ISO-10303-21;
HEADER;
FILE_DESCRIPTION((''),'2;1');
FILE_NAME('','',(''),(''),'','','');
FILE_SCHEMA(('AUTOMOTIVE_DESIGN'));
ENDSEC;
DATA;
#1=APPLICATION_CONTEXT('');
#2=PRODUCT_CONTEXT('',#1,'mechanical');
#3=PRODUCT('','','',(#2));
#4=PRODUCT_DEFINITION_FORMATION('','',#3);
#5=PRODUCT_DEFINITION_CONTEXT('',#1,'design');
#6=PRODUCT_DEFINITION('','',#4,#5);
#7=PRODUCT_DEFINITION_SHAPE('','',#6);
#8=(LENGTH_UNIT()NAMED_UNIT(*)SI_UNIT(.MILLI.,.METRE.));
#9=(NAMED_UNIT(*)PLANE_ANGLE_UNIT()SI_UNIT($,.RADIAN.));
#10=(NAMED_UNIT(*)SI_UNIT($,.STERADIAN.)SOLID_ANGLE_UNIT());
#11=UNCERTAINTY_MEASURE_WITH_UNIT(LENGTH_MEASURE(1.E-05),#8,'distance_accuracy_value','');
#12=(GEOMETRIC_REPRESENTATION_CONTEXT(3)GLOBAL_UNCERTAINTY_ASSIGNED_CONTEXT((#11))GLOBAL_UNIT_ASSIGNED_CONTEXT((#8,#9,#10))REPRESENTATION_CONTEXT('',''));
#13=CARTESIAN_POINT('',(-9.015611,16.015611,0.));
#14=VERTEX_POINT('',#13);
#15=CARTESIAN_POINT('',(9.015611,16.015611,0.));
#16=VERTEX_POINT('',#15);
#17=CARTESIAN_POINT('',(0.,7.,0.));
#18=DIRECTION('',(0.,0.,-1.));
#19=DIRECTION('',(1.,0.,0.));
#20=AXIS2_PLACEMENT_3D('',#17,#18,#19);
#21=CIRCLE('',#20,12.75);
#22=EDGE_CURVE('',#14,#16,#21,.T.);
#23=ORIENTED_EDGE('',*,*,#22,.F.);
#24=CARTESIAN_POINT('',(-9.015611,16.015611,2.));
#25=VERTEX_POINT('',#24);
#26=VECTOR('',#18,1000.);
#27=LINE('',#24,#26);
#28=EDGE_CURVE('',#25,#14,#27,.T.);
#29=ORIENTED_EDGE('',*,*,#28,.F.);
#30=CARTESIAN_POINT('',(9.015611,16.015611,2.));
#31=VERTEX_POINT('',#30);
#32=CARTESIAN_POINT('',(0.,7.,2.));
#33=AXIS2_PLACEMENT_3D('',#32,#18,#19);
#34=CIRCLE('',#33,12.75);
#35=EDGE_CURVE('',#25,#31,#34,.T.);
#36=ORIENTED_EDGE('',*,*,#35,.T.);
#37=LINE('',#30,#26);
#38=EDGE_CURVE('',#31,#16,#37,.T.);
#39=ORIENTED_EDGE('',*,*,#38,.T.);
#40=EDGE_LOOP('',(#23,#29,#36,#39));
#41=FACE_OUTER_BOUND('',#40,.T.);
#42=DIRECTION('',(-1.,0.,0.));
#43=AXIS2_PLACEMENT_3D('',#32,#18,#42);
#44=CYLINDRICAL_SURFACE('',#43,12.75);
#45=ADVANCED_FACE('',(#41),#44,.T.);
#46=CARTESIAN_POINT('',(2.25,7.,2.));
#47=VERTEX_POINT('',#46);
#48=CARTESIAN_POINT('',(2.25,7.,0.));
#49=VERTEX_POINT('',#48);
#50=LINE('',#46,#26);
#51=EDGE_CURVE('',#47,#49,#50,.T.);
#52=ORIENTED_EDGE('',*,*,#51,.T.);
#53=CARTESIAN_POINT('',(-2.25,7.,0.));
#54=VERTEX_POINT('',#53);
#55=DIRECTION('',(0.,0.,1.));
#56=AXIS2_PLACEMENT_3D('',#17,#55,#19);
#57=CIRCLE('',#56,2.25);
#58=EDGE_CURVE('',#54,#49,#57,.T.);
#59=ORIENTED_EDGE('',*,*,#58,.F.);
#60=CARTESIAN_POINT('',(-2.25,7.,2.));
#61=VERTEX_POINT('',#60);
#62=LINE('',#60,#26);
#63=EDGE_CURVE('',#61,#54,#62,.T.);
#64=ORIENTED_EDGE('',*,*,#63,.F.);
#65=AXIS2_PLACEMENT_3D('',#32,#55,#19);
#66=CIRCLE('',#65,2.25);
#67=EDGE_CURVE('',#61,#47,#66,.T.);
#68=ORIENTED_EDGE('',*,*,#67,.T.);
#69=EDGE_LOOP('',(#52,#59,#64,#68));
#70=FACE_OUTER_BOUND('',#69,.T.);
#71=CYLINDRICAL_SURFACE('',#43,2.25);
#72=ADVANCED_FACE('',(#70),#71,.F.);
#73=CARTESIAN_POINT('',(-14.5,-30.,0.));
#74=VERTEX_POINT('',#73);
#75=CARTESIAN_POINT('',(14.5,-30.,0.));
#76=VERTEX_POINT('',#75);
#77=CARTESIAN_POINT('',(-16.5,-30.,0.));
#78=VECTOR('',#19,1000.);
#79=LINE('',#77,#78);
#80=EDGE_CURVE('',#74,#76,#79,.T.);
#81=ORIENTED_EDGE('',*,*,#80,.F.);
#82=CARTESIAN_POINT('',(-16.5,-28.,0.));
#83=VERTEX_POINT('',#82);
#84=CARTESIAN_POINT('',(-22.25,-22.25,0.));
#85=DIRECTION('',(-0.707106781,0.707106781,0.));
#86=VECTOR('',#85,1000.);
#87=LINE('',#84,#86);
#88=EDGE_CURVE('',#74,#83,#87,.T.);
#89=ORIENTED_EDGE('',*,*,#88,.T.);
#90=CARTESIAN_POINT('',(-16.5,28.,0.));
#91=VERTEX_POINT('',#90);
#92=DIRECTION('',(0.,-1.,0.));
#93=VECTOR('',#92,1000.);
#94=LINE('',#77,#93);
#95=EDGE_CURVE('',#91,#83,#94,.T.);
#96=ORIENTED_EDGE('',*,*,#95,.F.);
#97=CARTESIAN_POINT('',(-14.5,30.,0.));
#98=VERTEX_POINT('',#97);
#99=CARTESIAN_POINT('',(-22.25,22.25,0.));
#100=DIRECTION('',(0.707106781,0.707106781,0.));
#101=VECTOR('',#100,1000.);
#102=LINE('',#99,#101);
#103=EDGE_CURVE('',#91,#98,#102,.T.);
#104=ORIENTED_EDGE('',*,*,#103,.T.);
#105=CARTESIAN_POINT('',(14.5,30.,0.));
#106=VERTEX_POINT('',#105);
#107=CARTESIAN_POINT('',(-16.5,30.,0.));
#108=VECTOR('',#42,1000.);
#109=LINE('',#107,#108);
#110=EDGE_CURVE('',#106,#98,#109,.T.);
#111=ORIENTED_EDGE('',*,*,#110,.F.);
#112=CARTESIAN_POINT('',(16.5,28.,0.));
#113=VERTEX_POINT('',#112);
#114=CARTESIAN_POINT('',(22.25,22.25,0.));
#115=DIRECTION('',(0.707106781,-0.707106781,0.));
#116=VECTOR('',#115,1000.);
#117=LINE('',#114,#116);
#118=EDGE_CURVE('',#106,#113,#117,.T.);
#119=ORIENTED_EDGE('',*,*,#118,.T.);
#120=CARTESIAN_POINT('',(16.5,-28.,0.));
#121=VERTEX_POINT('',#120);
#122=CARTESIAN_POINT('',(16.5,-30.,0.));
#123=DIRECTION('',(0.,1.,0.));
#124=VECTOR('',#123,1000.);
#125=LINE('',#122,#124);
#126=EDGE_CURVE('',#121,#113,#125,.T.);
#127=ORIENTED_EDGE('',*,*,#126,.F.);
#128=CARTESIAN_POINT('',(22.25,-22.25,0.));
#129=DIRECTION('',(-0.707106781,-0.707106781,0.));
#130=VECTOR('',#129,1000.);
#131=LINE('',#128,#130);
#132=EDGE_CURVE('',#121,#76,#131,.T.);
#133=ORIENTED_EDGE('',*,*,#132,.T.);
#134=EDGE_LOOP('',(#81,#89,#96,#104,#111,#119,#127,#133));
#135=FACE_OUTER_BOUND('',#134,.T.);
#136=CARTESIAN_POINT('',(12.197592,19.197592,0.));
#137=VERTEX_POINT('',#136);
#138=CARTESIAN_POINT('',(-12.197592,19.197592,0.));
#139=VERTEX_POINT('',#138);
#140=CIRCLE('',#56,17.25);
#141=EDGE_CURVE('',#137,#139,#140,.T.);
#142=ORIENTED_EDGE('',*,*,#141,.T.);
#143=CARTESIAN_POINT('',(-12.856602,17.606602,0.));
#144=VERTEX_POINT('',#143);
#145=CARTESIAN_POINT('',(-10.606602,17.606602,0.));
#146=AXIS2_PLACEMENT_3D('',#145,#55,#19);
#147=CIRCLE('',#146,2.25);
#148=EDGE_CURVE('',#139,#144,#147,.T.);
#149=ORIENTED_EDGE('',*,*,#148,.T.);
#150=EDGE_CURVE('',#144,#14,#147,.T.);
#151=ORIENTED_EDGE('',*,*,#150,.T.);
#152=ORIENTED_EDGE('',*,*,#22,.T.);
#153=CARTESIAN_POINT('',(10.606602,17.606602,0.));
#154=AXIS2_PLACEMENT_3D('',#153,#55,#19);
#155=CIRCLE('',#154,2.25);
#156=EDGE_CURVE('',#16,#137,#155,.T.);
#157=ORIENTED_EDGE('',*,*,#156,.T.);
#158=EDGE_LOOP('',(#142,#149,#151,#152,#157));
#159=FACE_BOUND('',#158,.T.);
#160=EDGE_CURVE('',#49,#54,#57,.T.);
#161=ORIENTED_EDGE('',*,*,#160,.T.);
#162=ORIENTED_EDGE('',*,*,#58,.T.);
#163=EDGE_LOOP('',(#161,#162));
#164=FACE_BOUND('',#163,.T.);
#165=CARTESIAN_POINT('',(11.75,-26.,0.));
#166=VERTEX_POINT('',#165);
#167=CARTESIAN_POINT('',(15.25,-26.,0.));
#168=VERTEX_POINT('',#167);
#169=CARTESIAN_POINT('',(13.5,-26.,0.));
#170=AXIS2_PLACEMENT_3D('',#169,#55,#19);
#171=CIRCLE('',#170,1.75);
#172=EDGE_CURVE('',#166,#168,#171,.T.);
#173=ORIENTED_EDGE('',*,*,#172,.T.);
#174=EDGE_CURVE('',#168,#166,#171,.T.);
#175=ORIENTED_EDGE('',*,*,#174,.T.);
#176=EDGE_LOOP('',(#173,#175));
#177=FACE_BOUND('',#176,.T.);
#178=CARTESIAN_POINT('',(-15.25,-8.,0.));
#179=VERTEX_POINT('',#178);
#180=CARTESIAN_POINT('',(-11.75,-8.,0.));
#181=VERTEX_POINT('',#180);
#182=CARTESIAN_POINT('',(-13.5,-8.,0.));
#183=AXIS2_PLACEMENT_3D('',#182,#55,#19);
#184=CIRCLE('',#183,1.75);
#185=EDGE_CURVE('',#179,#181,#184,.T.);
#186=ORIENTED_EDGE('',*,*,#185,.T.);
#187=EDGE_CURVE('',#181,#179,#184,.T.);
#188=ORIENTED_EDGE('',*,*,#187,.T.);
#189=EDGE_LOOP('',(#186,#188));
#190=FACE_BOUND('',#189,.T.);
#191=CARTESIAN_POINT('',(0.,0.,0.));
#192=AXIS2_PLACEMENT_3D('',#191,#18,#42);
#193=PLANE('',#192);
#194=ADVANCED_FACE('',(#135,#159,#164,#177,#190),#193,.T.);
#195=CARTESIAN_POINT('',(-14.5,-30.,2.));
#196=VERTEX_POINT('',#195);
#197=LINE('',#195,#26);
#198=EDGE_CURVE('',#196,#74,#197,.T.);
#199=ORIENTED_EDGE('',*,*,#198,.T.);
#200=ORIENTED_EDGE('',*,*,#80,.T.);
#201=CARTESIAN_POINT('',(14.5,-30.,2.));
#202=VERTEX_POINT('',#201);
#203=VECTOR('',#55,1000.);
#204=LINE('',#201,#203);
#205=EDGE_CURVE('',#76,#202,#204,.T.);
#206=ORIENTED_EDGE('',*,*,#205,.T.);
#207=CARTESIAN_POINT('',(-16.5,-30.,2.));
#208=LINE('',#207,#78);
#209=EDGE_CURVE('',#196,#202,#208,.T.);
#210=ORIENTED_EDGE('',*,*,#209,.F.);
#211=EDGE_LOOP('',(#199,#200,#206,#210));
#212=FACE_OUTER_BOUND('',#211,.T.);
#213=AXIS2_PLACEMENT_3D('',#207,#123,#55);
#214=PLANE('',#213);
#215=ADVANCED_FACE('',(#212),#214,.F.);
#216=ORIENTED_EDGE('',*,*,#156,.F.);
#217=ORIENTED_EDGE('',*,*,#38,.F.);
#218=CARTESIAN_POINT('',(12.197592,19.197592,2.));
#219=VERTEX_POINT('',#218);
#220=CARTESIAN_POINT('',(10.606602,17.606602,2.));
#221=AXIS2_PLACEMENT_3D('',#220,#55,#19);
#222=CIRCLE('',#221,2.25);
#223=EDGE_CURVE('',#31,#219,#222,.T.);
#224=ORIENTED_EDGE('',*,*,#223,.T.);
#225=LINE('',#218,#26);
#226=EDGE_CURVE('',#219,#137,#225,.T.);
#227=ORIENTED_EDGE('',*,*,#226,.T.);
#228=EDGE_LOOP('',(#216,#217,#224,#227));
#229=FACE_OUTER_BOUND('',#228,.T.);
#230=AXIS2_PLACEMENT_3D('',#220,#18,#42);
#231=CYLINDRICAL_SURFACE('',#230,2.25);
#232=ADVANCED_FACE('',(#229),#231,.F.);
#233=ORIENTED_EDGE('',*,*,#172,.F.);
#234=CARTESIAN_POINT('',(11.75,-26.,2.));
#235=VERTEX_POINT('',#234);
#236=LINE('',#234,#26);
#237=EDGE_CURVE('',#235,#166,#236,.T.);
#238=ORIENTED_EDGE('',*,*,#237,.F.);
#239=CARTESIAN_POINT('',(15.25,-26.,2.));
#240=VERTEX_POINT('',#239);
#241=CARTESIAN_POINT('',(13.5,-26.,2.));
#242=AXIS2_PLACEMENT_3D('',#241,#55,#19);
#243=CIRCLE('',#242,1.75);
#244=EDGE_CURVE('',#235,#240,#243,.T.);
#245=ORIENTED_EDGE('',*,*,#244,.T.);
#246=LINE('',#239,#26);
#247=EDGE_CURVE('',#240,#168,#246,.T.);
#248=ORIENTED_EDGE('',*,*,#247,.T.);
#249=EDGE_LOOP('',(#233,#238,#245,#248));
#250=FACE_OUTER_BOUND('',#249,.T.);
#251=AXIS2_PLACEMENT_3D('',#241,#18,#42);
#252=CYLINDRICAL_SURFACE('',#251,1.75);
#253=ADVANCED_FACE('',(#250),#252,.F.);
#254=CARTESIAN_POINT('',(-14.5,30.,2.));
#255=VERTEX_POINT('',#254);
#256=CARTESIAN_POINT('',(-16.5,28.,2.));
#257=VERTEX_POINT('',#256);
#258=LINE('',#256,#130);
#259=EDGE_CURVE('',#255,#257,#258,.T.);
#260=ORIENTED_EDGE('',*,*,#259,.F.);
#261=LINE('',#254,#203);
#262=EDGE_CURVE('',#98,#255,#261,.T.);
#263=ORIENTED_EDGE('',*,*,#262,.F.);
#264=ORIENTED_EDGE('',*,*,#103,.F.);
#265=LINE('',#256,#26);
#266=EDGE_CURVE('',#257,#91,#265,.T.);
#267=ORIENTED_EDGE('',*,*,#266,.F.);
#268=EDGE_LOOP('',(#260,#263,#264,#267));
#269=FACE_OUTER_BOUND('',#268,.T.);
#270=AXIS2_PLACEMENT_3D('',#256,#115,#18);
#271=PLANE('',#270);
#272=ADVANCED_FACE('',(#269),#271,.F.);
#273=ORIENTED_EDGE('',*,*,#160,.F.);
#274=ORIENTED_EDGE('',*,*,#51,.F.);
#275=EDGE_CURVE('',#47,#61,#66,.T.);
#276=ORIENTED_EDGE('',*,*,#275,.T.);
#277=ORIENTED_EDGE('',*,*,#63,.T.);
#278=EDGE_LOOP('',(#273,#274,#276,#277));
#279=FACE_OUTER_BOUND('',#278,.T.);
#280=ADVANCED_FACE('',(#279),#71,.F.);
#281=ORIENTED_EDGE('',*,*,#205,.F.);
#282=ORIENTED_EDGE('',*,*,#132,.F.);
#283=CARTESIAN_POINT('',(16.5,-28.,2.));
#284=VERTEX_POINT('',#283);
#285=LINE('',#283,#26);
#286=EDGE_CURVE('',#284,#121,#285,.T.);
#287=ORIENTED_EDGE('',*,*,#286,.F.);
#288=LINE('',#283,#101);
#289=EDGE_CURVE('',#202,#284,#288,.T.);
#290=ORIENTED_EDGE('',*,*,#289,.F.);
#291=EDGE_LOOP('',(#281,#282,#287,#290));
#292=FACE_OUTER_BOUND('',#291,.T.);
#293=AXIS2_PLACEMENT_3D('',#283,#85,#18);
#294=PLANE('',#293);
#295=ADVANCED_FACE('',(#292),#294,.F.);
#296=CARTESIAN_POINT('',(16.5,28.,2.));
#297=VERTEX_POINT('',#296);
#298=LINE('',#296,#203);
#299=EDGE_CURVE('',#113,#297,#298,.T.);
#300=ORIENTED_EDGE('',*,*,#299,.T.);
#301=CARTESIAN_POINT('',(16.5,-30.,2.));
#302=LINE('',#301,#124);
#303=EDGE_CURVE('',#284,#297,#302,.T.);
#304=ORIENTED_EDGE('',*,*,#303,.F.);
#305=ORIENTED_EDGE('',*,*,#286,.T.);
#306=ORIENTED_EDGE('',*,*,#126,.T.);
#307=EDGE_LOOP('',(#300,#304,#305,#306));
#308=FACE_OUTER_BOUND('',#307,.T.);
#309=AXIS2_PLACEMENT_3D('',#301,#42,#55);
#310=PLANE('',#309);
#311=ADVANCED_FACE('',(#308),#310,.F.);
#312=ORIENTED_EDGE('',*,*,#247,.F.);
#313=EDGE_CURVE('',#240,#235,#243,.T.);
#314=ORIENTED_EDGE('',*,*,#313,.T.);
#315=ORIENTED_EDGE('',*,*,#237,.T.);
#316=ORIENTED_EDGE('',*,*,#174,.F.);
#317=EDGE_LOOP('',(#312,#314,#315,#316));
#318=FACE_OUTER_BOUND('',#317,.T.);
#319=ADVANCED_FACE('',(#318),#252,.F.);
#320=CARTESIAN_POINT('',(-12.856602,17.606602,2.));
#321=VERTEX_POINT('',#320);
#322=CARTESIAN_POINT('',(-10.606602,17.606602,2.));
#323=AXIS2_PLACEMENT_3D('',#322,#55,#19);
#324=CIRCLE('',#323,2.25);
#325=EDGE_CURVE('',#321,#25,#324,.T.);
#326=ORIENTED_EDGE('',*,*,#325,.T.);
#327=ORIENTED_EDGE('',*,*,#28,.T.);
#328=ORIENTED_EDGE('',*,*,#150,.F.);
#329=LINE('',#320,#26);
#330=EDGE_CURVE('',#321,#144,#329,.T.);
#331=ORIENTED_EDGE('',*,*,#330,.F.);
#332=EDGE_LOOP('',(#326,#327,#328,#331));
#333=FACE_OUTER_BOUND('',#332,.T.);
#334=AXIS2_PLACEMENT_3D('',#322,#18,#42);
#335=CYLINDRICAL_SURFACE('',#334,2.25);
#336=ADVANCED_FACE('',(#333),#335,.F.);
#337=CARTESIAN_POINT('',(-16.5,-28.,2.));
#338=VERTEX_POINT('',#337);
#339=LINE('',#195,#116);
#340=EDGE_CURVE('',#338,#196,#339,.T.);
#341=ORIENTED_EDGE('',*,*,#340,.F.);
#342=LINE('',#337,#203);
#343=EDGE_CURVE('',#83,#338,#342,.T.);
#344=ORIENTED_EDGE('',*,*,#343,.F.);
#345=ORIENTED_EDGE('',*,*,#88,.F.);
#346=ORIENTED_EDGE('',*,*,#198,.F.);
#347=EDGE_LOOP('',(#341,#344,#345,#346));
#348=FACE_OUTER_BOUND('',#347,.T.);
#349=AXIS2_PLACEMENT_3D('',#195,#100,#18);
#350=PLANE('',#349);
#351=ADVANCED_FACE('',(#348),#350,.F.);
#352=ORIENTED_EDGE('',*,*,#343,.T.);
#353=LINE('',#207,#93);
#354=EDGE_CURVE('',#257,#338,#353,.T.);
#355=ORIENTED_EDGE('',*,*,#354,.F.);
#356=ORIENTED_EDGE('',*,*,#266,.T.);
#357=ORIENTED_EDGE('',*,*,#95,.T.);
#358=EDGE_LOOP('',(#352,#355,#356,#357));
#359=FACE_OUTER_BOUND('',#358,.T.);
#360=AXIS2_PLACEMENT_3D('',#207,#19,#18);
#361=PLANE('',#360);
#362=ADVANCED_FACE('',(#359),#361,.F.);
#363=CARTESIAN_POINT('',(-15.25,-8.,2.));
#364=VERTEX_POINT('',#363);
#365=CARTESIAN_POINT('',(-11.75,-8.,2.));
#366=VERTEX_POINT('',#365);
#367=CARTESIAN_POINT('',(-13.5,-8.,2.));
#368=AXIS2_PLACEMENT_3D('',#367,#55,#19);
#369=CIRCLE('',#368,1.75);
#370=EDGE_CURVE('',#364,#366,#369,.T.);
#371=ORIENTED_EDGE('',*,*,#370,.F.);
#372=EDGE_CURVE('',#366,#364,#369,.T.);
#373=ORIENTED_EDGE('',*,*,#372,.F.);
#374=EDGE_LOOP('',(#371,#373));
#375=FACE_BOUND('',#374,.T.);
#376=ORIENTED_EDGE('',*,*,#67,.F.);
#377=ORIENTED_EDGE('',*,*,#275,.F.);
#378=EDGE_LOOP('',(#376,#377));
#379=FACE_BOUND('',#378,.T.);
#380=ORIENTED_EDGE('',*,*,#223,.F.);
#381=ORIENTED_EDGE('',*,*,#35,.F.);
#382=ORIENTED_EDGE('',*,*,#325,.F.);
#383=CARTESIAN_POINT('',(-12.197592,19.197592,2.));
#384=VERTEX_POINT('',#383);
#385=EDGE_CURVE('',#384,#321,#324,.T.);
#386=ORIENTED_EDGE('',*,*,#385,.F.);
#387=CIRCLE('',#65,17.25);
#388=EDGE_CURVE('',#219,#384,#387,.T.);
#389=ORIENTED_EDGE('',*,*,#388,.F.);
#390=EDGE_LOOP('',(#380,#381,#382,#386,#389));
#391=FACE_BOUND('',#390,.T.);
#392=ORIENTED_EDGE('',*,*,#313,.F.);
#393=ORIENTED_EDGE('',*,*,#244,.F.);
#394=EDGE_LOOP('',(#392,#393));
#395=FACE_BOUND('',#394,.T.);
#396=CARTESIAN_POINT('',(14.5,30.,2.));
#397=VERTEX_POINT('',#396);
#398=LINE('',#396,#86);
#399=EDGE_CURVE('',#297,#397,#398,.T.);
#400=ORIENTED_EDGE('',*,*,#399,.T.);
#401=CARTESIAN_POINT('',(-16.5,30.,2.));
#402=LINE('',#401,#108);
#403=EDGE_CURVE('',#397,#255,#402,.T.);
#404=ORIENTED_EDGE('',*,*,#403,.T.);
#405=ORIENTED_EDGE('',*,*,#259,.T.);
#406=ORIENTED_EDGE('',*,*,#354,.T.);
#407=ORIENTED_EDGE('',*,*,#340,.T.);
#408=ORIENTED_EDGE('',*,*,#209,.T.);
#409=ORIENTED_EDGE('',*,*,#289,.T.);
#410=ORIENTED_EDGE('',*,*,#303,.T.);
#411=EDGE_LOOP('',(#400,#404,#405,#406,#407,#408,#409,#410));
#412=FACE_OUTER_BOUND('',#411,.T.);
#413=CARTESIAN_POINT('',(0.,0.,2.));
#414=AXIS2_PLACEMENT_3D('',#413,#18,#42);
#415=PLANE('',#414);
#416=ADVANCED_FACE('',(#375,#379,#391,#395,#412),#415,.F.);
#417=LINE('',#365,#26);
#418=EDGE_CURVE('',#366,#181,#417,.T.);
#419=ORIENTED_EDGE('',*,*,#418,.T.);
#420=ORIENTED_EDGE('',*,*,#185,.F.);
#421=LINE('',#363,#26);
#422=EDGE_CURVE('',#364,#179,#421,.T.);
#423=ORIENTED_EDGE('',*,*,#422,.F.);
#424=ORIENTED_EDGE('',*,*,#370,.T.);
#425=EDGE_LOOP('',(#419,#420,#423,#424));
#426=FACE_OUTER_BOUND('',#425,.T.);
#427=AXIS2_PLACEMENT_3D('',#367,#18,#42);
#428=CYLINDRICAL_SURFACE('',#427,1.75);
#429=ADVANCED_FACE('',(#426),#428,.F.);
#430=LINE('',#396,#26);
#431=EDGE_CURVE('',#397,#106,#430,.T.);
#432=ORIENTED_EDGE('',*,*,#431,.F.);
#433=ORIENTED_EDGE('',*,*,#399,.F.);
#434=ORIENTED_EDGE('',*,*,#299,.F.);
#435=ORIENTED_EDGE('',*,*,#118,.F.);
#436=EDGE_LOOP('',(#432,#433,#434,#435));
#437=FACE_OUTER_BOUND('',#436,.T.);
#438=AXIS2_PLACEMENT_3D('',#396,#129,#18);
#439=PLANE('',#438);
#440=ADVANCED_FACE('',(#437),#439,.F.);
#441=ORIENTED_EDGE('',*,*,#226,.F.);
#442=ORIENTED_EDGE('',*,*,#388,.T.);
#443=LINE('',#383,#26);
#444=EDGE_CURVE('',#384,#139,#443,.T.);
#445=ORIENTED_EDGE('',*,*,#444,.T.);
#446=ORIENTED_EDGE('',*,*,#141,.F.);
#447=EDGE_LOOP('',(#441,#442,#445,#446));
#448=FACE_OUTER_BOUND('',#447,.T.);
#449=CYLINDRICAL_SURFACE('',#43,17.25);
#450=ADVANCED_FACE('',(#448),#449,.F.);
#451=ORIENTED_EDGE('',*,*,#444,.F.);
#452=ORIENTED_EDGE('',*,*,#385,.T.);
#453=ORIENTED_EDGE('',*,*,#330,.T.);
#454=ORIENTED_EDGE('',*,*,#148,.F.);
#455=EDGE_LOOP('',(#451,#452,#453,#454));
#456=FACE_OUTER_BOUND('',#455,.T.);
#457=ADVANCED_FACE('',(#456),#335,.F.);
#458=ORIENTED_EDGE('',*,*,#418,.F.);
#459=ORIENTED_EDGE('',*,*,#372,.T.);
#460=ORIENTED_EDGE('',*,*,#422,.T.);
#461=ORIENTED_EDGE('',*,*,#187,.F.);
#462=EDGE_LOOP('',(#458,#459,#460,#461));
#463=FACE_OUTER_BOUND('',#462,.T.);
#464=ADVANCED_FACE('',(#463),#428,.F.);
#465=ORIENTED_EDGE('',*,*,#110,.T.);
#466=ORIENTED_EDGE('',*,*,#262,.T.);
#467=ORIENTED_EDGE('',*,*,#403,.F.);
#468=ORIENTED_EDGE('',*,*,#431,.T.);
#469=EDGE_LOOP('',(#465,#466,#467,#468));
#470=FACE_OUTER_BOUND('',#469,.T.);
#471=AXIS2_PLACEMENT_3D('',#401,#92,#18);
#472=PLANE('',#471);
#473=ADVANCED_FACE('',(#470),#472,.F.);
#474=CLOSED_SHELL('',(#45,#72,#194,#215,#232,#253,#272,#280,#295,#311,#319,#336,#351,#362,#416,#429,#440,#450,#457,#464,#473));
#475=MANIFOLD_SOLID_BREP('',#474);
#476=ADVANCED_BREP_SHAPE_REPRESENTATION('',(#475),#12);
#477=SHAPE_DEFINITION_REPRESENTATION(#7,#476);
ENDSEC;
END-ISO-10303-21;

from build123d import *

# Parameters (mm, degrees)
SKETCH1_W           = 33
SKETCH1_H           = 60
SKETCH1_R           = 2.25
SKETCH1_R_2         = 1.75
BOSS_EXTRUDE1_DEPTH = 2
CHAMFER1_SIZE       = 2


with BuildPart() as part:
    # Sketch1 → Boss-Extrude1 (new body)
    with BuildSketch(Plane.XY):
        Rectangle(SKETCH1_W, SKETCH1_H)
        with Locations((0, 7)):
            Circle(SKETCH1_R, mode=Mode.SUBTRACT)
        with Locations((13.5, -26)):
            Circle(SKETCH1_R_2, mode=Mode.SUBTRACT)
        with Locations((-13.5, -8)):
            Circle(SKETCH1_R_2, mode=Mode.SUBTRACT)
        with BuildLine():
            ThreePointArc((9.01561146, 16.01561146), (0, 19.75), (-9.01561146, 16.01561146))
            ThreePointArc((-9.01561146, 16.01561146), (-12.197591975, 16.01561146), (-12.197591975, 19.197591975))
            ThreePointArc((-12.197591975, 19.197591975), (0, 24.25), (12.197591975, 19.197591975))
            ThreePointArc((12.197591975, 19.197591975), (12.197591975, 16.01561146), (9.01561146, 16.01561146))
        make_face(mode=Mode.SUBTRACT)
    extrude(amount=BOSS_EXTRUDE1_DEPTH)

    # Chamfer1
    chamfer1_edges = [part.edges().sort_by_distance(p)[0] for p in [
        (16.5, -30, 1),
        (-16.5, -30, 1),
        (-16.5, 30, 1),
        (16.5, 30, 1),
    ]]
    chamfer(chamfer1_edges, length=CHAMFER1_SIZE)


solid = part.part
